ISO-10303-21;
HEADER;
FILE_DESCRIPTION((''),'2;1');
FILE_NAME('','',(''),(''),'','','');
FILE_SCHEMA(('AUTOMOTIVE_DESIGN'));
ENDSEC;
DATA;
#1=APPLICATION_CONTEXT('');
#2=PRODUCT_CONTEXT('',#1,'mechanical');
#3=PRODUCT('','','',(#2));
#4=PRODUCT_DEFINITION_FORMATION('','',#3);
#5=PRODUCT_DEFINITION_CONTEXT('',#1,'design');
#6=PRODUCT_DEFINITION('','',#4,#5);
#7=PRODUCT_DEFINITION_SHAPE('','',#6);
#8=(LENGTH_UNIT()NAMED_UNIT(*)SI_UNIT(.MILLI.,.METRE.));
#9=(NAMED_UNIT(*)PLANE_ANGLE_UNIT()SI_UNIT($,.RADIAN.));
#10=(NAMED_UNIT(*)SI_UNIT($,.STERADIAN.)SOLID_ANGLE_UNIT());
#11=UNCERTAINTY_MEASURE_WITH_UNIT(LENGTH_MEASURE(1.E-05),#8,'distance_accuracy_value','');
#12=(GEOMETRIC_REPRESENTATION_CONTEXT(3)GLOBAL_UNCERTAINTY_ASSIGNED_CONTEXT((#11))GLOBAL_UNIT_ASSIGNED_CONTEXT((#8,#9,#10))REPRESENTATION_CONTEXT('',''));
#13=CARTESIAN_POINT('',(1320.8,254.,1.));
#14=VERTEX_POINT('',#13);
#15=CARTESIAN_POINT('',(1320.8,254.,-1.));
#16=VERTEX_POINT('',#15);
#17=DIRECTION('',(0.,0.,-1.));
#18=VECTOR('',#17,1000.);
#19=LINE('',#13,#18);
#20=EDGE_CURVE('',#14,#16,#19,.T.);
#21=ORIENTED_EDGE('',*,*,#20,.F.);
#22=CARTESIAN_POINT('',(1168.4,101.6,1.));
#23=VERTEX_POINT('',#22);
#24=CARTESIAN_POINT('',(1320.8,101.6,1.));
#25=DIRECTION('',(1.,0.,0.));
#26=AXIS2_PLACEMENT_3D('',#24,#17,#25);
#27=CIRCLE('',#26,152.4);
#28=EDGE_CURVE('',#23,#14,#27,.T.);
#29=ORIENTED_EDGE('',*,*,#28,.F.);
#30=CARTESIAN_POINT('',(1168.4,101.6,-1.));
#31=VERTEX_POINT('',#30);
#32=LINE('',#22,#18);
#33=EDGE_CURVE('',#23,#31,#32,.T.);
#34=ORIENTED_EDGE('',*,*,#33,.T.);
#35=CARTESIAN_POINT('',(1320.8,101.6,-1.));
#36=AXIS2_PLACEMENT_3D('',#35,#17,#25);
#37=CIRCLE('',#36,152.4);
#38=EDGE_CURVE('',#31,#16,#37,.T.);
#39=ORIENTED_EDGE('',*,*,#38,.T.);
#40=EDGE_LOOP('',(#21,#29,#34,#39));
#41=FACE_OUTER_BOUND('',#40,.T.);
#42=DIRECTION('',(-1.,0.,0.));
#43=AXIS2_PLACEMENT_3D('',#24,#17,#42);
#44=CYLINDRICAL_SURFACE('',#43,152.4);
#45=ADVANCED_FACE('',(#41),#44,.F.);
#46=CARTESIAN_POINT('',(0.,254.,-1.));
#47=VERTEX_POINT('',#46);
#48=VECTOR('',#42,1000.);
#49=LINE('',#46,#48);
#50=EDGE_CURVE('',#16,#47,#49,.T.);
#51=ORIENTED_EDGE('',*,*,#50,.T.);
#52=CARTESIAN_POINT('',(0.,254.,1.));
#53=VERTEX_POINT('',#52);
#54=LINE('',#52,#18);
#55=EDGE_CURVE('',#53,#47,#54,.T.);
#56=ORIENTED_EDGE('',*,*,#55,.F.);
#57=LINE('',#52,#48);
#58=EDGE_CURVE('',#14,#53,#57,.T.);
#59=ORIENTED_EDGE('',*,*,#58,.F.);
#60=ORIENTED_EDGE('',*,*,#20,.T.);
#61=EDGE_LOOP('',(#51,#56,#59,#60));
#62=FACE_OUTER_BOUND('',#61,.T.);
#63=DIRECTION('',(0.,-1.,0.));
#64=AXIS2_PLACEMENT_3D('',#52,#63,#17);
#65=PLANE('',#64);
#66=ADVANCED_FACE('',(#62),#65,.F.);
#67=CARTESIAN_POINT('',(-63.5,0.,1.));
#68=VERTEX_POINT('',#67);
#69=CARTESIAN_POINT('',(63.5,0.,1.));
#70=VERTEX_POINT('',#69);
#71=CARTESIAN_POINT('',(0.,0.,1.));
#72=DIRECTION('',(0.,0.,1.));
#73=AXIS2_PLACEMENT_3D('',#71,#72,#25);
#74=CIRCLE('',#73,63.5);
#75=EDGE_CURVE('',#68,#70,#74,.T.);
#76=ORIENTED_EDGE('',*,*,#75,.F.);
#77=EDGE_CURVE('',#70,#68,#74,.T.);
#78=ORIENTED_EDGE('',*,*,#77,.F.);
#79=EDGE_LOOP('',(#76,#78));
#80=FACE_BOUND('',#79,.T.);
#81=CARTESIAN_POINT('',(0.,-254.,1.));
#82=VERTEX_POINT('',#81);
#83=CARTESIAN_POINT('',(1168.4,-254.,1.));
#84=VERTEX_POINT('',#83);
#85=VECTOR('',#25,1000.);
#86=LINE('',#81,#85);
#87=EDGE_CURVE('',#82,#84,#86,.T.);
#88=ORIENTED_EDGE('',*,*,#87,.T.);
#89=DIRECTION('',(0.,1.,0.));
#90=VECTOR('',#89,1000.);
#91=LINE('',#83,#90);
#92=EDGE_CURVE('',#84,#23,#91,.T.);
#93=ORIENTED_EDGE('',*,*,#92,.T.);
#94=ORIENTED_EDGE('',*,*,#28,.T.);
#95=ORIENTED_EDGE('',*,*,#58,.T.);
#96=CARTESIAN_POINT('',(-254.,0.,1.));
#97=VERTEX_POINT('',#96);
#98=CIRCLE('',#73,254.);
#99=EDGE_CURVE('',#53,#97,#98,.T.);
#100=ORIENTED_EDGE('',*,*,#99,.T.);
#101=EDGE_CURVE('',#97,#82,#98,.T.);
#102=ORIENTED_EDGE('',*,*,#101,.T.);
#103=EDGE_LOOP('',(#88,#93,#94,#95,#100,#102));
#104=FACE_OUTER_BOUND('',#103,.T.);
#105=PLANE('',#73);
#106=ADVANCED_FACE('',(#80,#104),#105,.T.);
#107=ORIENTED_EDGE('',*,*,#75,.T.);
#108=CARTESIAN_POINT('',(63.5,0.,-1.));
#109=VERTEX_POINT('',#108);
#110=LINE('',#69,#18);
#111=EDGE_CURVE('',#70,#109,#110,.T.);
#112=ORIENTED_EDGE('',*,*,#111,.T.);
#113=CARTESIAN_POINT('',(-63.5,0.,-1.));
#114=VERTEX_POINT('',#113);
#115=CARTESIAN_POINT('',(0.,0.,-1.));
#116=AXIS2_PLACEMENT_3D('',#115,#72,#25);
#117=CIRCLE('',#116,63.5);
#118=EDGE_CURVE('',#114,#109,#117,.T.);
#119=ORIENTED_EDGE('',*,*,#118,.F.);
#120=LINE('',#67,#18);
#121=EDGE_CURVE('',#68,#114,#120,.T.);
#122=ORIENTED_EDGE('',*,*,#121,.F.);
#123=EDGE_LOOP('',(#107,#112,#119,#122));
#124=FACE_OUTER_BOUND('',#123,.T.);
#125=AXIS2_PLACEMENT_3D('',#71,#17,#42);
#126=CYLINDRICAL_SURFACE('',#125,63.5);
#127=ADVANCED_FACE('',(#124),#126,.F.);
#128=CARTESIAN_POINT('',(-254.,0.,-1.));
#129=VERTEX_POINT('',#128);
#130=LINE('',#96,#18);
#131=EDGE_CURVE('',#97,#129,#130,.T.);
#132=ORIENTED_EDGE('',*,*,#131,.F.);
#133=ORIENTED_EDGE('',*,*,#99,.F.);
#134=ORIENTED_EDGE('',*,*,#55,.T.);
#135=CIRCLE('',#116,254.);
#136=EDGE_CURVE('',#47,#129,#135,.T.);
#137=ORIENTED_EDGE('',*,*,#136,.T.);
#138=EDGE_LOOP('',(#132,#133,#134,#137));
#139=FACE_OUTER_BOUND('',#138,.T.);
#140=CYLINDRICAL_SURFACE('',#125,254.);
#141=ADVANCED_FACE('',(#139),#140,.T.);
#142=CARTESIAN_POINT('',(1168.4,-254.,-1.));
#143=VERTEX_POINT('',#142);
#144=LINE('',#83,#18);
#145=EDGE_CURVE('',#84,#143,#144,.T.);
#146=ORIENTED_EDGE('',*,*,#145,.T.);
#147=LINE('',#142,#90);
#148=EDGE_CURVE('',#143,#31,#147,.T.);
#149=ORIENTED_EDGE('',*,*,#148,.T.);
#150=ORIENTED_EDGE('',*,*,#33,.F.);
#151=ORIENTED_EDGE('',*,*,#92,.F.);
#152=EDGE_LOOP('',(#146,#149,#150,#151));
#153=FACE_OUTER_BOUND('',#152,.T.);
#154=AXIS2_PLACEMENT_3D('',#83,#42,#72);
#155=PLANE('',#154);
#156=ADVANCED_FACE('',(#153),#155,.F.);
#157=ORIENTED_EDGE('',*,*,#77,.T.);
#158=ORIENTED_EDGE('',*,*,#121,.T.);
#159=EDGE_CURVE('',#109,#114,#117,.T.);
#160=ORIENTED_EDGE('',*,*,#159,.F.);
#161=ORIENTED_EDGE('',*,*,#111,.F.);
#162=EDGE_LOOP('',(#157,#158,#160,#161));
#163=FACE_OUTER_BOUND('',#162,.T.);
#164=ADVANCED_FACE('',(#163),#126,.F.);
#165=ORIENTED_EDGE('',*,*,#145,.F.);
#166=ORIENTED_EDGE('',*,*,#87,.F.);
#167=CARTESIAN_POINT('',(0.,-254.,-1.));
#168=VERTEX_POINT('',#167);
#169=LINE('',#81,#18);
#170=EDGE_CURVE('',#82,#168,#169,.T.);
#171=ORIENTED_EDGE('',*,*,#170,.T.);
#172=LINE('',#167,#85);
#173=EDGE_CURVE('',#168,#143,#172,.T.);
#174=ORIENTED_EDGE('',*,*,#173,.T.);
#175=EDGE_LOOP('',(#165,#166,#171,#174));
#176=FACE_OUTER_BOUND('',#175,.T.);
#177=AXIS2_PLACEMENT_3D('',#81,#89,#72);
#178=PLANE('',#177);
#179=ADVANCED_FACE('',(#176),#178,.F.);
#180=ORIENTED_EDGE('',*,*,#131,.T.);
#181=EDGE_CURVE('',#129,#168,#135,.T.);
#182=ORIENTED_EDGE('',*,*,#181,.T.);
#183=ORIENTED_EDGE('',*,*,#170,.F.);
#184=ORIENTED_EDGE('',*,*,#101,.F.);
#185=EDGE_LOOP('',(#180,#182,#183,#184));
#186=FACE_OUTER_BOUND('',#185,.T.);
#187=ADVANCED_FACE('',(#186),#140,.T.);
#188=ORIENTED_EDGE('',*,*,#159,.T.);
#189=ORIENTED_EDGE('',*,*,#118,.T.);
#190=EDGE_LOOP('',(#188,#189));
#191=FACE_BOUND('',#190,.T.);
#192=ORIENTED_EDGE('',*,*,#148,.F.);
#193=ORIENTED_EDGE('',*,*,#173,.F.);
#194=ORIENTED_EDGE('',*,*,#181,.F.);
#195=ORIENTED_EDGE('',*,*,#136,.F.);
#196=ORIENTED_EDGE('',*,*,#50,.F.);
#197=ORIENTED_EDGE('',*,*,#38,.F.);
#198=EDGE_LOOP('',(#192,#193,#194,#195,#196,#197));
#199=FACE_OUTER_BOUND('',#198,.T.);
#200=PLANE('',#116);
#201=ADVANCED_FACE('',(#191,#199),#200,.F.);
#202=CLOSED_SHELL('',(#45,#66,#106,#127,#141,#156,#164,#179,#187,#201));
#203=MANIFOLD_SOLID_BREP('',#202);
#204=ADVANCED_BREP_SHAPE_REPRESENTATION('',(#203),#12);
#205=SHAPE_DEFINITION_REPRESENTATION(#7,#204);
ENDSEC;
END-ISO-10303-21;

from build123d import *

# Parameters (mm, degrees)
SKETCH1_R           = 63.5
BOSS_EXTRUDE1_DEPTH = 1


with BuildPart() as part:
    # Sketch1 → Boss-Extrude1 (new, symmetric)
    with BuildSketch(Plane.XY):
        with BuildLine():
            Line((0, 254), (1320.8, 254))
            ThreePointArc((1320.8, 254), (1213.036926547, 209.363073453), (1168.4, 101.6))
            Line((1168.4, 101.6), (1168.4, -254))
            Line((1168.4, -254), (0, -254))
            ThreePointArc((0, -254), (-254, 0), (0, 254))
        make_face()
        Circle(SKETCH1_R, mode=Mode.SUBTRACT)
    extrude(amount=BOSS_EXTRUDE1_DEPTH, both=True)


solid = part.part
